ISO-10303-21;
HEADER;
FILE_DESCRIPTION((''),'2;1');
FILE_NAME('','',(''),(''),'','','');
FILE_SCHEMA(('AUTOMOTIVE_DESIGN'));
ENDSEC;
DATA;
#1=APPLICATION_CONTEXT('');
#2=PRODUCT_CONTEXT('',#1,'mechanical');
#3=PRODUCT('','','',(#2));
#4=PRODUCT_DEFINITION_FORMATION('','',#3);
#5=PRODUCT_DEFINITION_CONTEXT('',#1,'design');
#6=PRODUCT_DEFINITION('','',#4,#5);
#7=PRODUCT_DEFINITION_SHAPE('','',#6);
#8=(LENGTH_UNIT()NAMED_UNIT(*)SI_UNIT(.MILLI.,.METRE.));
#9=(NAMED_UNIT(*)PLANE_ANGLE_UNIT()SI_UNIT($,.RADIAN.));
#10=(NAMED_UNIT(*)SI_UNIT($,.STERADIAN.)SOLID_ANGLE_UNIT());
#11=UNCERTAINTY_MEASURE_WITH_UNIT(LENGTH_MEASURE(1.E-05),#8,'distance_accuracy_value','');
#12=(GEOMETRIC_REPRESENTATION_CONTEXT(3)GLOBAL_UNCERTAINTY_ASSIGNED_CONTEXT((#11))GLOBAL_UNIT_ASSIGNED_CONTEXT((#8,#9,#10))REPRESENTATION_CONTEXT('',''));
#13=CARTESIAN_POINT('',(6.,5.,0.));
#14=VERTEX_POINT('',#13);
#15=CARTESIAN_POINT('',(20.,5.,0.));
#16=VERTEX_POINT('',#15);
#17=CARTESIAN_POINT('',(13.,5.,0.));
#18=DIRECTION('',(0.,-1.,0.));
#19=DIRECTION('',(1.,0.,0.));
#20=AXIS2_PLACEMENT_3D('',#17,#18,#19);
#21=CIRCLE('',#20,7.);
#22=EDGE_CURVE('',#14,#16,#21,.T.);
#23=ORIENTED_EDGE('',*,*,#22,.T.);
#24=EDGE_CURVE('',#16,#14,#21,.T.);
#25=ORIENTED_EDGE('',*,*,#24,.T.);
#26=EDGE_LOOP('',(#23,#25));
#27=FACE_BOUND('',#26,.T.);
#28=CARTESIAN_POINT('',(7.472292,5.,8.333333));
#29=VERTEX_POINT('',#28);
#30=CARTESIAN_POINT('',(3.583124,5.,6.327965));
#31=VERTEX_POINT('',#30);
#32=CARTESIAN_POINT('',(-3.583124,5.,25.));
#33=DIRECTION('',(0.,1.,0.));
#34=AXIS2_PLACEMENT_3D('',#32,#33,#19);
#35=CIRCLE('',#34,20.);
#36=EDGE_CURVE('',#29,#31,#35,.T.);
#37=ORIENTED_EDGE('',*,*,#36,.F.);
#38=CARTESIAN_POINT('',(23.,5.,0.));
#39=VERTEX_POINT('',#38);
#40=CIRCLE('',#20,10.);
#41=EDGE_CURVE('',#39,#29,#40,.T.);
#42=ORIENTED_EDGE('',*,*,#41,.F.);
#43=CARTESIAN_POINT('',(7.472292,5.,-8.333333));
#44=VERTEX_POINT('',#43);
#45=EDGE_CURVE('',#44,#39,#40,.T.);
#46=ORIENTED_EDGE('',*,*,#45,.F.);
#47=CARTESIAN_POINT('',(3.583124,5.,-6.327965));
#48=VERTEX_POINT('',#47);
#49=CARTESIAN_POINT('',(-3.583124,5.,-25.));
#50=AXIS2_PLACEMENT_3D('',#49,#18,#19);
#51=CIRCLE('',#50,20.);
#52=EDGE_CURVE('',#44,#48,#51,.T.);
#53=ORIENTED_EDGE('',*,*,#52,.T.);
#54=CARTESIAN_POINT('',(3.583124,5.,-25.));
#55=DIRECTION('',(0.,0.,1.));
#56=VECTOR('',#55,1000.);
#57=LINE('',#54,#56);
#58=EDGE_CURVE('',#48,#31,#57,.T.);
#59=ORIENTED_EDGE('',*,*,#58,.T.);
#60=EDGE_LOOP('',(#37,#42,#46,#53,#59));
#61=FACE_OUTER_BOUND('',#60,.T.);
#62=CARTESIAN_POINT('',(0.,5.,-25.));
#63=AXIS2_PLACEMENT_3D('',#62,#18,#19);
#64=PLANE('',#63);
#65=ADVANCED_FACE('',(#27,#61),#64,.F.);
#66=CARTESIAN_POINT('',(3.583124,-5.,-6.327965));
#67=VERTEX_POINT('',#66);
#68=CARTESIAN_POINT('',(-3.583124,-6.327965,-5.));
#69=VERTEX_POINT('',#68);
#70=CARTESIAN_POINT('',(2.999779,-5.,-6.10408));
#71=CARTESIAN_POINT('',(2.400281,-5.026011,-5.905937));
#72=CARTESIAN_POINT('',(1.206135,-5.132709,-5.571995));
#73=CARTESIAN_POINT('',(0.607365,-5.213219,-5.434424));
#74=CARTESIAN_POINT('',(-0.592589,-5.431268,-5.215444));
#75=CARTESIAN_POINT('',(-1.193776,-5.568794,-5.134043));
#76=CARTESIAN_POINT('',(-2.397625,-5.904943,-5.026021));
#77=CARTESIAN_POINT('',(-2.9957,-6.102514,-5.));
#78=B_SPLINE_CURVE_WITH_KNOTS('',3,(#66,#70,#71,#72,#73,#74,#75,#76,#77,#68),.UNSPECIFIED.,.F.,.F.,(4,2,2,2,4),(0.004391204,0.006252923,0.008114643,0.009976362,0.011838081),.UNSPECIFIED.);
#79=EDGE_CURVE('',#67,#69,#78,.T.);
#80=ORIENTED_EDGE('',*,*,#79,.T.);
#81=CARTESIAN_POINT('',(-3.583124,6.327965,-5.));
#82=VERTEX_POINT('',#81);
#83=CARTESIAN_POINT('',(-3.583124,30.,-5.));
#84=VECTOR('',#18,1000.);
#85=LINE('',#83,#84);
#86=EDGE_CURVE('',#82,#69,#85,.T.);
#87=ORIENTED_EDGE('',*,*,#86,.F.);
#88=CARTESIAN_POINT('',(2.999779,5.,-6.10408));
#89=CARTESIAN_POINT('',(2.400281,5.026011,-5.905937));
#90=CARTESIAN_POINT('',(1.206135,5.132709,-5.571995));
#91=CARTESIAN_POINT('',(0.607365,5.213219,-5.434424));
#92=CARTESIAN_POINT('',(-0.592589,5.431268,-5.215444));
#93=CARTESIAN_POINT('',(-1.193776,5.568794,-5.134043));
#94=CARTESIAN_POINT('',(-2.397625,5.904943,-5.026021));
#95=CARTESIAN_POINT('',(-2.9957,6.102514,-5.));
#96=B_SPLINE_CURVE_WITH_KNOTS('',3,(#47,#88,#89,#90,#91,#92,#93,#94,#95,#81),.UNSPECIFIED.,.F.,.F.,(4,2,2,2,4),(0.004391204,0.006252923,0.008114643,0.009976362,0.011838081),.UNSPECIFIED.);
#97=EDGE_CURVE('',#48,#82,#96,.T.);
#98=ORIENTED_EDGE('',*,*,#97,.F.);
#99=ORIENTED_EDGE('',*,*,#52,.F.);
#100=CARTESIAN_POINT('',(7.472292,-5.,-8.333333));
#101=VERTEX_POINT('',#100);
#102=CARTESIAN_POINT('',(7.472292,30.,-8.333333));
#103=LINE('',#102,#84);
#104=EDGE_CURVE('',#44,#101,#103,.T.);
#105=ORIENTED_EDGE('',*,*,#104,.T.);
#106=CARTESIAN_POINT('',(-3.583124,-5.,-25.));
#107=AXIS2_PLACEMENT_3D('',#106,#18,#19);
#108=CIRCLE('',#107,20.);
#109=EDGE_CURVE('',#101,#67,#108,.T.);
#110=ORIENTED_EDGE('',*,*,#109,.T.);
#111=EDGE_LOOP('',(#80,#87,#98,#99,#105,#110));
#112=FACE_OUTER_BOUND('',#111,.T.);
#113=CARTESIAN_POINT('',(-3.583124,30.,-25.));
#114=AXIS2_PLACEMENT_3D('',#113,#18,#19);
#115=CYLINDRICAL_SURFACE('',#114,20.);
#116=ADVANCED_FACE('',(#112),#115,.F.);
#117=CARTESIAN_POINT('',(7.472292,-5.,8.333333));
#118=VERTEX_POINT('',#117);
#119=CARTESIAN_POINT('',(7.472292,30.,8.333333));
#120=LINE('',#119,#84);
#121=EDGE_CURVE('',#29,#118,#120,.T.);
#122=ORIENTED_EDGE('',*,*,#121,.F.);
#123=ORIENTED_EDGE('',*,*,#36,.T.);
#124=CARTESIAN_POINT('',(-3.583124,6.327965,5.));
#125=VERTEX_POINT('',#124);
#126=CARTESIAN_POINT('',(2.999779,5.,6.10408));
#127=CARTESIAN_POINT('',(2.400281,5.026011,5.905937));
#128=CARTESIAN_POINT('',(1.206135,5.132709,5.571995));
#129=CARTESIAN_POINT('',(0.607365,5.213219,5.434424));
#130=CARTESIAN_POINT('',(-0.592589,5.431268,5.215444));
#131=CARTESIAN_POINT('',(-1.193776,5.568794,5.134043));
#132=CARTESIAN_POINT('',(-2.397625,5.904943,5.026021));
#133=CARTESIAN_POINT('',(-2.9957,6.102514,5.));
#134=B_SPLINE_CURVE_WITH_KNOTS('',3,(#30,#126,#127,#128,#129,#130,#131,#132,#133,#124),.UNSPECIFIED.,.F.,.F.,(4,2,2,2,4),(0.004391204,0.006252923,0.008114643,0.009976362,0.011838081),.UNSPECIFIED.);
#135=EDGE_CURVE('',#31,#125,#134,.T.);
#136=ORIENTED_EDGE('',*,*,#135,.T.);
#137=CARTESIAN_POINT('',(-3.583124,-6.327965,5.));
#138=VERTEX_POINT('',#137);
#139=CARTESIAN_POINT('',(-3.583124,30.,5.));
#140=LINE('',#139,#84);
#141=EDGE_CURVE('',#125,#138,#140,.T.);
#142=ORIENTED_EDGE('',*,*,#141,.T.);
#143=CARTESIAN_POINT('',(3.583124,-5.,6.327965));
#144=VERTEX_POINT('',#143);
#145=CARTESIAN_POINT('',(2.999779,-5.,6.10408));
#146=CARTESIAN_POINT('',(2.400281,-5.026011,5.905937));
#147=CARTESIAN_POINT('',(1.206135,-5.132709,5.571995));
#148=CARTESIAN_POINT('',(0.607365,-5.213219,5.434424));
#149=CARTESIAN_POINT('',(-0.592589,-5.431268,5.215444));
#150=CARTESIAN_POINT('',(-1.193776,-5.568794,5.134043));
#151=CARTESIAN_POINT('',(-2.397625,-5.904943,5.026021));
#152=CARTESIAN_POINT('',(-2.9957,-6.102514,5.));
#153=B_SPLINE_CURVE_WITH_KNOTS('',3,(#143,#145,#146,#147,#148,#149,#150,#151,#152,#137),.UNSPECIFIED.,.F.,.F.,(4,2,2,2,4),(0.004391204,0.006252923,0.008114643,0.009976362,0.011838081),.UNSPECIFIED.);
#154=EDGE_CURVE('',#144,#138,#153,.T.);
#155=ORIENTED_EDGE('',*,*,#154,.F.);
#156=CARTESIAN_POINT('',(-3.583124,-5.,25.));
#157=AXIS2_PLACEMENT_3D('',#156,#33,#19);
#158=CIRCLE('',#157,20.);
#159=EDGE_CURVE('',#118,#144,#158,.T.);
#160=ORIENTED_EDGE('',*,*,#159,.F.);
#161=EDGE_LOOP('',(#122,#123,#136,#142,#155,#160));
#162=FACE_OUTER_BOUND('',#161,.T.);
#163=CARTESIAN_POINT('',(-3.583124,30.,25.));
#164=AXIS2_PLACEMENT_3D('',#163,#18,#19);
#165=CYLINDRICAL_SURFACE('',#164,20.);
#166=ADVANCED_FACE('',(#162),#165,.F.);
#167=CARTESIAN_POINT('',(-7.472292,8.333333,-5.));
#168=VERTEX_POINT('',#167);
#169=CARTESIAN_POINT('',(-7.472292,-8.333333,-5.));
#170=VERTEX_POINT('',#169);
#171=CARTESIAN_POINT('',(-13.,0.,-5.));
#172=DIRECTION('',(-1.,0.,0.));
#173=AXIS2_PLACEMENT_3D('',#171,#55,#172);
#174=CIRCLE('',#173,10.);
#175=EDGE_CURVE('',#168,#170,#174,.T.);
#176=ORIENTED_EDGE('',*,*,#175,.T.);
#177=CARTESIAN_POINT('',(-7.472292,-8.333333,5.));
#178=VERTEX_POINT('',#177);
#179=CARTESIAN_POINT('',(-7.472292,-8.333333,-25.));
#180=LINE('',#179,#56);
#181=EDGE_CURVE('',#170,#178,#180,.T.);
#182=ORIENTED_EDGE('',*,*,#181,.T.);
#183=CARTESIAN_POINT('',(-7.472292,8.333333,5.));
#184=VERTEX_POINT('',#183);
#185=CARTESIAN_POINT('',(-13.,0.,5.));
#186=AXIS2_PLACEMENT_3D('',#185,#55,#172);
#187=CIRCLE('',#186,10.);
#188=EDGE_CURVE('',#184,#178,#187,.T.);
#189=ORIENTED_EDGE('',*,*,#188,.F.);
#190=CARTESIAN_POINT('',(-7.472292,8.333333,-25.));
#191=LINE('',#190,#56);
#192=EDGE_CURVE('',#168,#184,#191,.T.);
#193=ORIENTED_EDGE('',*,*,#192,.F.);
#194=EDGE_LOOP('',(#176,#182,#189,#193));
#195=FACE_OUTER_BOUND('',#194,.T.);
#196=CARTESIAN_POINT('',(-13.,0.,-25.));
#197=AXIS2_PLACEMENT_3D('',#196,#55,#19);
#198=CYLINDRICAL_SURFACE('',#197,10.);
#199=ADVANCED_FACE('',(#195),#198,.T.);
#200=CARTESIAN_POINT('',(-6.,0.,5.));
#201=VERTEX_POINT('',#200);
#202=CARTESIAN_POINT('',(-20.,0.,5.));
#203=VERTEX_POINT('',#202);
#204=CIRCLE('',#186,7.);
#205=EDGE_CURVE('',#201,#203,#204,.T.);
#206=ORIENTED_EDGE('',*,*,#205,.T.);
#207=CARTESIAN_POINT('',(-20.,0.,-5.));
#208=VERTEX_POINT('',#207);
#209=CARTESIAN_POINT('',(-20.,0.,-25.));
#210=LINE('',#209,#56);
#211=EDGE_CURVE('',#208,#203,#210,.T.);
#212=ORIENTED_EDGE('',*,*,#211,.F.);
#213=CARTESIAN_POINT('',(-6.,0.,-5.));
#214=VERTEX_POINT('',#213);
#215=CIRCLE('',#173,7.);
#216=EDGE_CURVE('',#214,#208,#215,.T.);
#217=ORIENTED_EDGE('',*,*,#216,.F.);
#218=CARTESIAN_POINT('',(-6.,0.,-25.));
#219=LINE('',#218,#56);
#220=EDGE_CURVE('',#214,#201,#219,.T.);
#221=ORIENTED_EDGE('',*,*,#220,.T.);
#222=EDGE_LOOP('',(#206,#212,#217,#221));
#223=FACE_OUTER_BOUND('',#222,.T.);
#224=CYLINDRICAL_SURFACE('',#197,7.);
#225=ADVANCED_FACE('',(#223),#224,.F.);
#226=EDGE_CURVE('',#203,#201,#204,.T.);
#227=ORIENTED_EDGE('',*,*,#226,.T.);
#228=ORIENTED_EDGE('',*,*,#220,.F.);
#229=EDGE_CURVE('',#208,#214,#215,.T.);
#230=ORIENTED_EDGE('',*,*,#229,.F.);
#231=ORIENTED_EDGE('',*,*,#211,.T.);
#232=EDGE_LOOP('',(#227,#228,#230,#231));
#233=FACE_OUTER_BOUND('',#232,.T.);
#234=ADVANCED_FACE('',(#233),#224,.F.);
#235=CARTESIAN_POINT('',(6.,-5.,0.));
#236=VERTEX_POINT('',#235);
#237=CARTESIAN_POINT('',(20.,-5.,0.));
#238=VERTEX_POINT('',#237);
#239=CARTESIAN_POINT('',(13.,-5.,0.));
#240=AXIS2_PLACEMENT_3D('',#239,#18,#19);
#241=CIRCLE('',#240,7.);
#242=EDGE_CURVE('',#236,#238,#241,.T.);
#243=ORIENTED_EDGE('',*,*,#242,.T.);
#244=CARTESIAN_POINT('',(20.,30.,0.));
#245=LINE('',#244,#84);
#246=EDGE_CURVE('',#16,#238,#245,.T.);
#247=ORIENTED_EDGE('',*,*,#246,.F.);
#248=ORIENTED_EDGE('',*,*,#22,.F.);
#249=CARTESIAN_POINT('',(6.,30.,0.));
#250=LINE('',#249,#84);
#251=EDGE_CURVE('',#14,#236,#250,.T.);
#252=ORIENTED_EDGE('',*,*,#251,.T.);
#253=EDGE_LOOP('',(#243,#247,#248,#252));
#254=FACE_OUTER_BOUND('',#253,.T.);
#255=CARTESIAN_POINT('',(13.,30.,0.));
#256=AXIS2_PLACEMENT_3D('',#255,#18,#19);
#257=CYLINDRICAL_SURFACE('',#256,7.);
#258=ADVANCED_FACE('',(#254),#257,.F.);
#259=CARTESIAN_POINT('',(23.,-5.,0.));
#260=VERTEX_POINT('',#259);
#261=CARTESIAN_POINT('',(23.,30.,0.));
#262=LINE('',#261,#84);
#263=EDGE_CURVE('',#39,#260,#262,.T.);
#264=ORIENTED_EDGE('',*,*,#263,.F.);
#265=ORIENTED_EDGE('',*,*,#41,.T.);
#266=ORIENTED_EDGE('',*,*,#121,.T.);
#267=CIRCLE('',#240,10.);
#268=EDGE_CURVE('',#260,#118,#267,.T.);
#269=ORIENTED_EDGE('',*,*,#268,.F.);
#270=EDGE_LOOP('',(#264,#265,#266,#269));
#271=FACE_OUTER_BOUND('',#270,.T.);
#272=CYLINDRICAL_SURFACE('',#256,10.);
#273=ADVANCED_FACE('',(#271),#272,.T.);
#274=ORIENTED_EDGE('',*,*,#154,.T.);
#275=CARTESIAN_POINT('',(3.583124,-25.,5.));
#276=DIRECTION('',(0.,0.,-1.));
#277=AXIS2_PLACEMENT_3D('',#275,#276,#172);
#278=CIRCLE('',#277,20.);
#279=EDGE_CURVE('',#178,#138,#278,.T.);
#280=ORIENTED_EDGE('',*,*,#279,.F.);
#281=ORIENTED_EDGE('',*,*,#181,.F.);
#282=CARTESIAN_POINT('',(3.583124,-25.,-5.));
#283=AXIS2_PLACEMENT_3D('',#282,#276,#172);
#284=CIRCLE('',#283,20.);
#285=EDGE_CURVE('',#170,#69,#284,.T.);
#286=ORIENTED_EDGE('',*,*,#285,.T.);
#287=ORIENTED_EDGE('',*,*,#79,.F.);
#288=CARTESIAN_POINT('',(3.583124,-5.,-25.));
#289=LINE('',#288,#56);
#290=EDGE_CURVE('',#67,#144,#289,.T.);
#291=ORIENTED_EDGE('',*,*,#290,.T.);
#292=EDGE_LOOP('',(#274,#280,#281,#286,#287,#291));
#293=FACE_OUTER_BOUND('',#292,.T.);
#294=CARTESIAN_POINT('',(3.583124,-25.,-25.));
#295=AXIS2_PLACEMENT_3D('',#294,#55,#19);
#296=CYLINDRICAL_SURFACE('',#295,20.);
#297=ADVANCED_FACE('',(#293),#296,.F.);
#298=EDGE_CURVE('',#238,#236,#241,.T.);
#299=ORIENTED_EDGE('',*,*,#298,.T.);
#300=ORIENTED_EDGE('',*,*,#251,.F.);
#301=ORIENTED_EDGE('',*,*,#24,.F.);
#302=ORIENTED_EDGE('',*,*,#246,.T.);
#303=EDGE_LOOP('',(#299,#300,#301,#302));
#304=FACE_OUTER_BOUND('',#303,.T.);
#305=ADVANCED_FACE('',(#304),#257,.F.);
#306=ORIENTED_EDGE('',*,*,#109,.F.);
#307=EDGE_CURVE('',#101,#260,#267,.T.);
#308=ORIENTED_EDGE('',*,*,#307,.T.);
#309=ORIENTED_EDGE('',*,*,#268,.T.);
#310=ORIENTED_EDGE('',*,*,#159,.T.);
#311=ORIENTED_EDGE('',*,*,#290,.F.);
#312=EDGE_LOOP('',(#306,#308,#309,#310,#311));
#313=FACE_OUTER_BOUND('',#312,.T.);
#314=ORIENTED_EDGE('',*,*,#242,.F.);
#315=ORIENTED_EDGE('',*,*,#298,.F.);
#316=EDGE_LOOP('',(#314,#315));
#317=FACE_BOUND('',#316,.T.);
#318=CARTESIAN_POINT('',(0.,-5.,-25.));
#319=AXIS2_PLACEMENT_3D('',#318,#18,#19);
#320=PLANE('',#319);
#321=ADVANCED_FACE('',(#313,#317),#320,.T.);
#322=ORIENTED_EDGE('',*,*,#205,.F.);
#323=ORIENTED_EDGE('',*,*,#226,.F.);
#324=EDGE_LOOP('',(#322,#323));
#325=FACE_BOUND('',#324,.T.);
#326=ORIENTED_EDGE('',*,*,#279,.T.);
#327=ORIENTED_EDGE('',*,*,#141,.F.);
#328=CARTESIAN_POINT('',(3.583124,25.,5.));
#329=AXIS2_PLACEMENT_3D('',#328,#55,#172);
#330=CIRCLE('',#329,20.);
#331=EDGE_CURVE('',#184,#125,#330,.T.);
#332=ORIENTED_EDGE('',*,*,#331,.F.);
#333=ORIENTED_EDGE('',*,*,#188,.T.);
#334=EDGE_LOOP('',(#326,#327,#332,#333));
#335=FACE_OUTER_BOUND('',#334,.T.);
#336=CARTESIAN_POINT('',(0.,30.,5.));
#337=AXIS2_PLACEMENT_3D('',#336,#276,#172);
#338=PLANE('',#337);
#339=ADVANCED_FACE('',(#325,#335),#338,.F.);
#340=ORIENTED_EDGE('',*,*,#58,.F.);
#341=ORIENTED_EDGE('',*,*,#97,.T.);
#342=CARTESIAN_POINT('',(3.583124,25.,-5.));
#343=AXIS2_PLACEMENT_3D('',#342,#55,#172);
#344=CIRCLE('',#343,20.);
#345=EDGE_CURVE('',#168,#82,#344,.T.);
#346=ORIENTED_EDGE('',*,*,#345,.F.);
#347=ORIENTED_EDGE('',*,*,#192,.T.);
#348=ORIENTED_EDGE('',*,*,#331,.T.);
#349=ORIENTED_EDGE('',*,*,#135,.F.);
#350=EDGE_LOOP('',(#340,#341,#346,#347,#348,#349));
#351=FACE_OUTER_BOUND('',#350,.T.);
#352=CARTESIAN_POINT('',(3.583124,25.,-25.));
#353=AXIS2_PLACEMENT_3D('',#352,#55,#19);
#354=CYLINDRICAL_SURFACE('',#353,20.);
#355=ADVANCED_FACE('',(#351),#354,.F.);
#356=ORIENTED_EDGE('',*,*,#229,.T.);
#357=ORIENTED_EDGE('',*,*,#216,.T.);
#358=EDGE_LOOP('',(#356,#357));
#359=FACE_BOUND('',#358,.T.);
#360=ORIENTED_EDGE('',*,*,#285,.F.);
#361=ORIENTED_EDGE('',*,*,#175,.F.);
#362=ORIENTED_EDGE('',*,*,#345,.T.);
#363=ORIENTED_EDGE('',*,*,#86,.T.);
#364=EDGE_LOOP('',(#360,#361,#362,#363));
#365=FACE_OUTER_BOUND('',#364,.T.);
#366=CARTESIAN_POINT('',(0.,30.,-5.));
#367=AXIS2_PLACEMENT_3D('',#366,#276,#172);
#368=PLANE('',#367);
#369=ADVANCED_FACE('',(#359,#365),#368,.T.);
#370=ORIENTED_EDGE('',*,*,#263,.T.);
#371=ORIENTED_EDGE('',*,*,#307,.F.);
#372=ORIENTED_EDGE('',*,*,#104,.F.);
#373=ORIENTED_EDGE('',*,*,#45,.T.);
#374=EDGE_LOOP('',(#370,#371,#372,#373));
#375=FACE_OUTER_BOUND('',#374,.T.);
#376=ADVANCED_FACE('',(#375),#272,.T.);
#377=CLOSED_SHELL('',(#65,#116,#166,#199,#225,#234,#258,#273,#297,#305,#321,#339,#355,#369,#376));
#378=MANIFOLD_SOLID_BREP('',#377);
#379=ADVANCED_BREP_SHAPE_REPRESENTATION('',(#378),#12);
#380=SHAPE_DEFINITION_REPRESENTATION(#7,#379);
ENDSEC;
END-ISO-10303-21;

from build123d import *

# Parameters (mm, degrees)
LINK_BLOCK_SKETCH_W               = 46
LINK_BLOCK_SKETCH_H               = 20
LINK_BLOCK_DEPTH                  = 10
FIRST_LUG_PROFILE_SKETCH_R        = 7
FIRST_LUG_PROFILE_BORE_CUT_DEPTH  = 35
SECOND_LUG_PROFILE_SKETCH_W       = 55.121968116
SECOND_LUG_PROFILE_SKETCH_H       = 28.549832612
SECOND_LUG_PROFILE_SKETCH_R       = 7
SECOND_LUG_PROFILE_BORE_CUT_DEPTH = 35


with BuildPart() as part:
    # Link Block Sketch → Link Block (new, symmetric)
    with BuildSketch(Plane.XY):
        Rectangle(LINK_BLOCK_SKETCH_W, LINK_BLOCK_SKETCH_H)
    extrude(amount=LINK_BLOCK_DEPTH, both=True)

    # First Lug Profile Sketch → First Lug Profile & Bore Cut (cut, symmetric)
    with BuildSketch(Plane.XY.offset(10)):
        with BuildLine():
            ThreePointArc((-7.472292016, 8.333333333), (-2.19037874, 5.851457845), (3.583123952, 5))
            Line((3.583123952, 5), (23, 5))
            Line((23, 5), (23, 10))
            Line((23, 10), (-13, 10))
            ThreePointArc((-13, 10), (-10.113248654, 9.574271078), (-7.472292016, 8.333333333))
        make_face()
        with BuildLine():
            ThreePointArc((-23, -4.3e-08), (-20.071067827, 7.071067797), (-13, 10))
            Line((-13, 10), (-23, 10))
            Line((-23, 10), (-23, -4.3e-08))
        make_face()
        with BuildLine():
            ThreePointArc((-13, -10), (-20.071067797, -7.071067827), (-23, -4.3e-08))
            Line((-23, -4.3e-08), (-23, -10))
            Line((-23, -10), (-13, -10))
        make_face()
        with BuildLine():
            Line((23, -10), (23, -5))
            Line((23, -5), (3.583123952, -5))
            ThreePointArc((3.583123952, -5), (-2.19037874, -5.851457845), (-7.472292016, -8.333333333))
            ThreePointArc((-7.472292016, -8.333333333), (-10.113248654, -9.574271078), (-13, -10))
            Line((-13, -10), (23, -10))
        make_face()
        with Locations((-13, 0)):
            Circle(FIRST_LUG_PROFILE_SKETCH_R)
    extrude(amount=FIRST_LUG_PROFILE_BORE_CUT_DEPTH, both=True, mode=Mode.SUBTRACT)

    # Second Lug Profile Sketch → Second Lug Profile & Bore Cut (cut, symmetric)
    # profile 1 of 6: a face of its own
    with BuildSketch(Plane.XZ.offset(5)):
        with Locations((1.394530012, 1.140979101)):
            Rectangle(SECOND_LUG_PROFILE_SKETCH_W, SECOND_LUG_PROFILE_SKETCH_H)
        with BuildLine():
            Line((-23, -5), (-23, 5))
            Line((-23, 5), (-3.583123952, 5))
            ThreePointArc((-3.583123952, 5), (0.06100146, 5.334793416), (3.583123952, 6.327965002))
            Line((3.583123952, 6.327965002), (3.583123952, 10))
            Line((3.583123952, 10), (13, 10))
            Line((13, 10), (23, 10))
            Line((23, 10), (23, -6e-08))
            Line((23, -6e-08), (23, -10))
            Line((23, -10), (12.999999984, -10))
            Line((12.999999984, -10), (3.583123952, -10))
            Line((3.583123952, -10), (3.583123952, -6.327965002))
            ThreePointArc((3.583123952, -6.327965002), (0.06100146, -5.334793416), (-3.583123952, -5))
            Line((-3.583123952, -5), (-23, -5))
        make_face(mode=Mode.SUBTRACT)
    # profile 2 of 6: a face of its own
    with BuildSketch(Plane.XZ.offset(5)):
        with Locations((13, 0)):
            Circle(SECOND_LUG_PROFILE_SKETCH_R)
    # profile 3 of 6: a face of its own
    with BuildSketch(Plane.XZ.offset(5)):
        with BuildLine():
            Line((23, -10), (23, -6e-08))
            ThreePointArc((23, -6e-08), (20.071067785, -7.071067839), (12.999999984, -10))
            Line((12.999999984, -10), (23, -10))
        make_face()
    # profile 4 of 6: a face of its own
    with BuildSketch(Plane.XZ.offset(5)):
        with BuildLine():
            ThreePointArc((7.472292016, -8.333333333), (5.582716659, -7.223966531), (3.583123952, -6.327965002))
            Line((3.583123952, -6.327965002), (3.583123952, -10))
            Line((3.583123952, -10), (12.999999984, -10))
            ThreePointArc((12.999999984, -10), (10.113248646, -9.574271075), (7.472292016, -8.333333333))
        make_face()
    # profile 5 of 6: a face of its own
    with BuildSketch(Plane.XZ.offset(5)):
        with BuildLine():
            Line((3.583123952, 10), (3.583123952, 6.327965002))
            ThreePointArc((3.583123952, 6.327965002), (5.582716659, 7.223966531), (7.472292016, 8.333333333))
            ThreePointArc((7.472292016, 8.333333333), (10.113248654, 9.574271078), (13, 10))
            Line((13, 10), (3.583123952, 10))
        make_face()
    # profile 6 of 6: a face of its own
    with BuildSketch(Plane.XZ.offset(5)):
        with BuildLine():
            Line((23, 10), (13, 10))
            ThreePointArc((13, 10), (20.071067833, 7.071067791), (23, -6e-08))
            Line((23, -6e-08), (23, 10))
        make_face()
    extrude(amount=SECOND_LUG_PROFILE_BORE_CUT_DEPTH, both=True, mode=Mode.SUBTRACT)


solid = part.part
